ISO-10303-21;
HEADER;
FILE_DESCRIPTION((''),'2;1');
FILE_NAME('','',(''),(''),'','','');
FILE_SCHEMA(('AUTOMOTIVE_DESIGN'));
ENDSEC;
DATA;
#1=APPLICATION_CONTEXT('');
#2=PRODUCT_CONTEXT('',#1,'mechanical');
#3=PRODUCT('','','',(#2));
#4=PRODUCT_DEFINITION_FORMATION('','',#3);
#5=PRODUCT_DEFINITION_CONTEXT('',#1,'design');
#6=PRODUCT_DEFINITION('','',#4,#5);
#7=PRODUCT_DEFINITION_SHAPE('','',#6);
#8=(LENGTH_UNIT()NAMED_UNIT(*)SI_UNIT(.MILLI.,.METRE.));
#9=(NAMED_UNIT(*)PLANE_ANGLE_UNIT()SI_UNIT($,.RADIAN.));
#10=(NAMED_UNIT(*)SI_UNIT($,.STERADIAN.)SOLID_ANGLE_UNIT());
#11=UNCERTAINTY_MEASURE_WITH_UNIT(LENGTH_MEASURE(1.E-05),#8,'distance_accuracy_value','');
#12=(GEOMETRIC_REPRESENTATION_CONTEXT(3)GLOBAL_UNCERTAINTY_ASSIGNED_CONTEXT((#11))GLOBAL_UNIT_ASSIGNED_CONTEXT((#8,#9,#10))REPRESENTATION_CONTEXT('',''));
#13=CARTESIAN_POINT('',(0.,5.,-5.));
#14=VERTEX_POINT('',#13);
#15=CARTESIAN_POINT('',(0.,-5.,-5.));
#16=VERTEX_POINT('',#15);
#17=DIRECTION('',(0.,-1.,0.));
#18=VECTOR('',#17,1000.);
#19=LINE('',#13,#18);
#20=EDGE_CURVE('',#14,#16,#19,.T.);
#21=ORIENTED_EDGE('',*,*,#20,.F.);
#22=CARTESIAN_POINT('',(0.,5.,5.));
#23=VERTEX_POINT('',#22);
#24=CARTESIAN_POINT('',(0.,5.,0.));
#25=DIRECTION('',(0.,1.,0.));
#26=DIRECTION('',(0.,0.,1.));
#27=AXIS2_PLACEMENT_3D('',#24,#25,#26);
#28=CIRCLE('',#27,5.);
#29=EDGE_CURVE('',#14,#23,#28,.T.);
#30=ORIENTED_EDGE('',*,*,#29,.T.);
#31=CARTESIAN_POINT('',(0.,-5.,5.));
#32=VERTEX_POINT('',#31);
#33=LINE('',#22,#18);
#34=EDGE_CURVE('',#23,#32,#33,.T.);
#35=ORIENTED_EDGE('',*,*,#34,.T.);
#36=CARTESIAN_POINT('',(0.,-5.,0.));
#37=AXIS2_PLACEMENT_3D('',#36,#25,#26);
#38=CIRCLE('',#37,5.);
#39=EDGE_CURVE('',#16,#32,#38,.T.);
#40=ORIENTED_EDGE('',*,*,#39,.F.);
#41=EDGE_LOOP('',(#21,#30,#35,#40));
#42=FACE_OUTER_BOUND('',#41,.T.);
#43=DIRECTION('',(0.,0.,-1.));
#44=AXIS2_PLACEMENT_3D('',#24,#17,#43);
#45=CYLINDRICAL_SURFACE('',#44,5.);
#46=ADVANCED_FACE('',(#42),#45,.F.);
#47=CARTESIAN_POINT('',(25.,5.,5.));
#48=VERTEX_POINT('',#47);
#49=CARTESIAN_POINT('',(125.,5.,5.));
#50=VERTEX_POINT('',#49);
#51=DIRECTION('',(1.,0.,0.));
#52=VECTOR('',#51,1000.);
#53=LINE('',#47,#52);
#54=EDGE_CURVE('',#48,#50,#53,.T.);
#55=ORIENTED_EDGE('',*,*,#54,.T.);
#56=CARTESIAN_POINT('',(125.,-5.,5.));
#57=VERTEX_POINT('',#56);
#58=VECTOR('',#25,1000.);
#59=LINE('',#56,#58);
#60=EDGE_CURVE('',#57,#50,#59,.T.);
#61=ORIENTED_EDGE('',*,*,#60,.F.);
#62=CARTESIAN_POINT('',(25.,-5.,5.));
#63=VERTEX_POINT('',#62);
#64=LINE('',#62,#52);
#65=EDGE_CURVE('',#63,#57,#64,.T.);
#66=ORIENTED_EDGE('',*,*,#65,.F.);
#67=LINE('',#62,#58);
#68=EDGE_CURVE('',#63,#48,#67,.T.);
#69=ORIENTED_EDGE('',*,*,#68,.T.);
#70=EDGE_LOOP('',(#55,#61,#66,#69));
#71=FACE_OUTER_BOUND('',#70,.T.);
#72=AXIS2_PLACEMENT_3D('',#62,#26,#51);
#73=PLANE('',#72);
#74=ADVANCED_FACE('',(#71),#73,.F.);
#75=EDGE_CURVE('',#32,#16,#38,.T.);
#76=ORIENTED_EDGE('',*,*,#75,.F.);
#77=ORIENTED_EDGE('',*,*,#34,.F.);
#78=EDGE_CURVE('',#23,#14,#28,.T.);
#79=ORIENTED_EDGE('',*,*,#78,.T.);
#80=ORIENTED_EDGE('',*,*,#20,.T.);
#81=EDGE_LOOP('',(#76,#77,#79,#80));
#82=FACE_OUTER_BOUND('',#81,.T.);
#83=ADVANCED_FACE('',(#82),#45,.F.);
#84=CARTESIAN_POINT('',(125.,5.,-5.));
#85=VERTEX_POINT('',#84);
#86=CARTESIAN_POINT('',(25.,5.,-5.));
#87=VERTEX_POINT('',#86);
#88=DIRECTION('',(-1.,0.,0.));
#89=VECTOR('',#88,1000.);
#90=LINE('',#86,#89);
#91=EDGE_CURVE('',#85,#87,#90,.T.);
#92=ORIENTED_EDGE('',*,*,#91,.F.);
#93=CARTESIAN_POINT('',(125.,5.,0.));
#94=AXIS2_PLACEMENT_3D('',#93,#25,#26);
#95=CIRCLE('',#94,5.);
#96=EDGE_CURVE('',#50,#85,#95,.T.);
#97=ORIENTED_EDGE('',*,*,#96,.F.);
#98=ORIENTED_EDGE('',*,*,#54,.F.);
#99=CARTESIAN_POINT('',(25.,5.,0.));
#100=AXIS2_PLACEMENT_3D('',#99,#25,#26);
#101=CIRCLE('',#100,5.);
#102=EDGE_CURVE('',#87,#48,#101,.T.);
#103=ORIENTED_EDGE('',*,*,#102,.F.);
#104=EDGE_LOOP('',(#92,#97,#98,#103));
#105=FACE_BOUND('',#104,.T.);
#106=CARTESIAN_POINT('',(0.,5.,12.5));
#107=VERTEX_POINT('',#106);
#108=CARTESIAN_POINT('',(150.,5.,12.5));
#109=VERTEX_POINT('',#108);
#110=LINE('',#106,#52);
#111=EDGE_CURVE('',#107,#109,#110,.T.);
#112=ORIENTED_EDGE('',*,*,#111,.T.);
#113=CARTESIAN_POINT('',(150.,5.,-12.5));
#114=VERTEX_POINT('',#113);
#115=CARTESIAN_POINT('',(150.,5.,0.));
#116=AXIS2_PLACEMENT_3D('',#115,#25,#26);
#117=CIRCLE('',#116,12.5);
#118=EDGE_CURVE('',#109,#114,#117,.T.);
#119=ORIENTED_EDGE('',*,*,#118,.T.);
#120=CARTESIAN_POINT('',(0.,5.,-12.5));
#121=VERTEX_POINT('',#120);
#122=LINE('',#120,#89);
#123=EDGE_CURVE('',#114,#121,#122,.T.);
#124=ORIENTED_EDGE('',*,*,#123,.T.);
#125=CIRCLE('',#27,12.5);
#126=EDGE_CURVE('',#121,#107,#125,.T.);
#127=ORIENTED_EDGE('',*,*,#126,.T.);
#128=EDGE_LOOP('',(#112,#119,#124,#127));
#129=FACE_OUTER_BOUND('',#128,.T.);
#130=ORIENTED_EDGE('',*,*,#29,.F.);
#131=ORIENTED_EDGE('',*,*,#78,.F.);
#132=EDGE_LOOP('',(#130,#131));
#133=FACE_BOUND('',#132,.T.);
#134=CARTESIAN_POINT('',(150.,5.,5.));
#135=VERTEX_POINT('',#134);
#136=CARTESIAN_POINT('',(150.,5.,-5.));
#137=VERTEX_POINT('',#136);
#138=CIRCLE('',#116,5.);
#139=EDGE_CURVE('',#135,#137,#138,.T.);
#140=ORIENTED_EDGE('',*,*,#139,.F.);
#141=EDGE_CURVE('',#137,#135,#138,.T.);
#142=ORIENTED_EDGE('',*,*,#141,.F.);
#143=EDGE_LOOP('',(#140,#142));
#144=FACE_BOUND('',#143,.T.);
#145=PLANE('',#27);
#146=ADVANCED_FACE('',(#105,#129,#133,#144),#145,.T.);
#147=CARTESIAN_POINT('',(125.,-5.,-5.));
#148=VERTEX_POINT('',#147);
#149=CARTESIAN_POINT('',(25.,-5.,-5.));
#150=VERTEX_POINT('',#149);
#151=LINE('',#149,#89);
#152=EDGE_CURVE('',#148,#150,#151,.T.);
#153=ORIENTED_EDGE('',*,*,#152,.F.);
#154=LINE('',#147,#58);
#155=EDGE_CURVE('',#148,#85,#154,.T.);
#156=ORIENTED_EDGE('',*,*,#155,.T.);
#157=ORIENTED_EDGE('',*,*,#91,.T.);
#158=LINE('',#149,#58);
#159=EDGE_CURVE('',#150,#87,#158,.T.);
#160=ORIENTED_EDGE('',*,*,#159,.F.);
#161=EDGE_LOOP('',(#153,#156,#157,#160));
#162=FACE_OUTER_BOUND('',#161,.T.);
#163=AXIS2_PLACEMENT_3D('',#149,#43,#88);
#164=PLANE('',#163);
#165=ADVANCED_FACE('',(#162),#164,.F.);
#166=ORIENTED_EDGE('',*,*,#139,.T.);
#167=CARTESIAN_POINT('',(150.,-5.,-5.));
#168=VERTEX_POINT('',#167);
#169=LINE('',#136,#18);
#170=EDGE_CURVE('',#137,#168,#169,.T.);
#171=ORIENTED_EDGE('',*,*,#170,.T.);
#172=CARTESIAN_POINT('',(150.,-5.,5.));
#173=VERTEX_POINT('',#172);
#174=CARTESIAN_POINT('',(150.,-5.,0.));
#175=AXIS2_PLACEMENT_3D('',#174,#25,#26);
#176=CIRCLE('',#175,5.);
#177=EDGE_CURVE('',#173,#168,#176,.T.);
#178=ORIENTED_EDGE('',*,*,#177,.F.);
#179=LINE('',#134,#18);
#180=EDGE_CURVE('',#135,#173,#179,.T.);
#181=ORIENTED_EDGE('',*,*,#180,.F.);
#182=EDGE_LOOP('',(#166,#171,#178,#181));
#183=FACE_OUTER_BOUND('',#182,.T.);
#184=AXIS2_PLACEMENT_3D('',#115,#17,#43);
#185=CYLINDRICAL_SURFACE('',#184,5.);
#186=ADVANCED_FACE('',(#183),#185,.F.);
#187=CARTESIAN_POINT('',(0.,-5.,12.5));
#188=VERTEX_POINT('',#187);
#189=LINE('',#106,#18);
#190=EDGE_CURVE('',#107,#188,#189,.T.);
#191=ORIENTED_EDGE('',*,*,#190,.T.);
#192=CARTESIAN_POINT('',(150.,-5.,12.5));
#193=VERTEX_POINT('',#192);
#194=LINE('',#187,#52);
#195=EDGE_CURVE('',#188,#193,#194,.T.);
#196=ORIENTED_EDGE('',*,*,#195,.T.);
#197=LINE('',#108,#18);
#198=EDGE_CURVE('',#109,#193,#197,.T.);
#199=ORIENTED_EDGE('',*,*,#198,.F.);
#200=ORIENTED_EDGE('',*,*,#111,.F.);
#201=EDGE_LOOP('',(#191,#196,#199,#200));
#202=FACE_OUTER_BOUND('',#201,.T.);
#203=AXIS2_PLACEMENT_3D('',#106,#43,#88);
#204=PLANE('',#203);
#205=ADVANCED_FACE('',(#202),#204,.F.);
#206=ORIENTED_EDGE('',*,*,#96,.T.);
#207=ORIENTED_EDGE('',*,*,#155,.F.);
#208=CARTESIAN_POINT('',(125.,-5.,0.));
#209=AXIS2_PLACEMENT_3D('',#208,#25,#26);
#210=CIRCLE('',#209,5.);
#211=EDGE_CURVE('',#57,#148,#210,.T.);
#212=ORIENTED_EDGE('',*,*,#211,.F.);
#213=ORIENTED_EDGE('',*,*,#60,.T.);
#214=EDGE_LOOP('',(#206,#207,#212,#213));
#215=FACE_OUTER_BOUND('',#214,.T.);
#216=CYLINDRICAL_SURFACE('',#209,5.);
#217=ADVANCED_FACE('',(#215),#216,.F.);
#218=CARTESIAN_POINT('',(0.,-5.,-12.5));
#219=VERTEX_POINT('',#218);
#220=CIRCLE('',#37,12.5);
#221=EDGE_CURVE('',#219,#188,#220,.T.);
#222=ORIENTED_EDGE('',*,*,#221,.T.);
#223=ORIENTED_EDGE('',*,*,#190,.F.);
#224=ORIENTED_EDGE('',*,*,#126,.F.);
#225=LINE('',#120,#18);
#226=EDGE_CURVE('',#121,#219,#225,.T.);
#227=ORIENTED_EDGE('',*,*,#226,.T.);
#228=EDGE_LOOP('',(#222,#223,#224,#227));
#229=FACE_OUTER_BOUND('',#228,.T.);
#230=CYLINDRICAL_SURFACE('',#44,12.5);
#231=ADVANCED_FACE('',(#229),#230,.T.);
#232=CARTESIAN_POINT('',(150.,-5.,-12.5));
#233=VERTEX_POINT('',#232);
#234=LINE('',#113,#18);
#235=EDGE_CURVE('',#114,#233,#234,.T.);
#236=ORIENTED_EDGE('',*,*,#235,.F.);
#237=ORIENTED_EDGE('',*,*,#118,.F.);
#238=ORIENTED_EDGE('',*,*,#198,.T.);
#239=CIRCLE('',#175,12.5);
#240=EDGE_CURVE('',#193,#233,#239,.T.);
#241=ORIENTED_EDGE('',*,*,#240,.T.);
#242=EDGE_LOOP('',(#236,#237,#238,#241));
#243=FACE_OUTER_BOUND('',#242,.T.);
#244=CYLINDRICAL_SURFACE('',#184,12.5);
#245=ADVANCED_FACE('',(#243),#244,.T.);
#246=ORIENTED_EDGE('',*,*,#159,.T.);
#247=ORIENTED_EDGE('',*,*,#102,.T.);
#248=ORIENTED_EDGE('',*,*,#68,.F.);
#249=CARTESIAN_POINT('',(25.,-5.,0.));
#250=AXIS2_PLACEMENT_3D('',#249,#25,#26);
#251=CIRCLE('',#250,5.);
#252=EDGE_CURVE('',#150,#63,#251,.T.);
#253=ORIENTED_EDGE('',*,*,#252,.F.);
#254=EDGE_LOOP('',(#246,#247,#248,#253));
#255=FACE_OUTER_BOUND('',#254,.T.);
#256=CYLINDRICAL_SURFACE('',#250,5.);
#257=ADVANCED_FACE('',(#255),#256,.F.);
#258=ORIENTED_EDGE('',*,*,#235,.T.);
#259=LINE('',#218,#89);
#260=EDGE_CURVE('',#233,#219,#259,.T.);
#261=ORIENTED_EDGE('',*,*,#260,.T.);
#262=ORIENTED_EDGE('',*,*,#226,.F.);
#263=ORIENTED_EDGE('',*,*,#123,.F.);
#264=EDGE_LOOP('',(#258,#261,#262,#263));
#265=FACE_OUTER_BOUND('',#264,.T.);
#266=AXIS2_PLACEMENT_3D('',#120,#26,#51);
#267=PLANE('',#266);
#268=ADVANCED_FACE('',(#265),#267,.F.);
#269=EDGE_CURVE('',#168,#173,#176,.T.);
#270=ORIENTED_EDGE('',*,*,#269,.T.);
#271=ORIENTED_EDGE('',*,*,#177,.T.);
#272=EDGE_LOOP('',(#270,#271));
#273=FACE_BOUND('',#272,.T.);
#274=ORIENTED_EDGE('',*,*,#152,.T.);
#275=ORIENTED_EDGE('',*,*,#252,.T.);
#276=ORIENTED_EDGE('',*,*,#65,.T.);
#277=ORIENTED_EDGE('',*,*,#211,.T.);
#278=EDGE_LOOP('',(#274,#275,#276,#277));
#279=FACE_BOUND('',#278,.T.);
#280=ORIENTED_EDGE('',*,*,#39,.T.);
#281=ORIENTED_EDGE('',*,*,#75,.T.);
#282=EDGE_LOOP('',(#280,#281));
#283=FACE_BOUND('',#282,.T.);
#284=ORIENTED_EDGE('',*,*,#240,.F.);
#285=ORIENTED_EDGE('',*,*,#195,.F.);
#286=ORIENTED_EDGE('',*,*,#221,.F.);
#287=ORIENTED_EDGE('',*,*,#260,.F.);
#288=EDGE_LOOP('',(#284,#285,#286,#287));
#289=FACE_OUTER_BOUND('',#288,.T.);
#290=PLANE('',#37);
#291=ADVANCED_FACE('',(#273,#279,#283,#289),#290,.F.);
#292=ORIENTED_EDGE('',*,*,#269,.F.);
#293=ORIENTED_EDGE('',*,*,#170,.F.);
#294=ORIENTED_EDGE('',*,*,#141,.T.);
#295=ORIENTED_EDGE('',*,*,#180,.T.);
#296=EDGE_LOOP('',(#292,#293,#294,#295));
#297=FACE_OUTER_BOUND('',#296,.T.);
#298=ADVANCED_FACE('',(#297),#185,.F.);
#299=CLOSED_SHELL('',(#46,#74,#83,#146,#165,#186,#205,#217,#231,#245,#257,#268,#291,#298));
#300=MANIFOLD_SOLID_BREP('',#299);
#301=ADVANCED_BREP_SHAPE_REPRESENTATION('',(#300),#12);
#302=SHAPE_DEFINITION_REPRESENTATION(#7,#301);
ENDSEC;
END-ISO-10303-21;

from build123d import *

# Parameters (mm, degrees)
SKETCH1_R           = 5
BOSS_EXTRUDE1_DEPTH = 5
CUT_EXTRUDE1_DEPTH  = 10


with BuildPart() as part:
    # Sketch1 → Boss-Extrude1 (new, symmetric)
    with BuildSketch(Plane(origin=(0, 0, 0), x_dir=(1, 0, 0), z_dir=(0, 1, 0))):
        with BuildLine():
            Line((0, 12.5), (150, 12.5))
            ThreePointArc((150, 12.5), (162.5, 0), (150, -12.5))
            Line((150, -12.5), (0, -12.5))
            ThreePointArc((0, -12.5), (-12.5, 0), (0, 12.5))
        make_face()
        with Locations(Location((0, 0, 0), (0, 0, 270))):
            Circle(SKETCH1_R, mode=Mode.SUBTRACT)
        with Locations(Location((150, 0, 0), (0, 0, 270))):
            Circle(SKETCH1_R, mode=Mode.SUBTRACT)
    extrude(amount=BOSS_EXTRUDE1_DEPTH, both=True)

    # Sketch2 → Cut-Extrude1 (cut)
    with BuildSketch(Plane(origin=(0, 5, 0), x_dir=(1, 0, 0), z_dir=(0, 1, 0))):
        with BuildLine():
            Line((25, 5), (125, 5))
            ThreePointArc((125, 5), (130, 0), (125, -5))
            Line((125, -5), (25, -5))
            ThreePointArc((25, -5), (20, 0), (25, 5))
        make_face()
    extrude(amount=-CUT_EXTRUDE1_DEPTH, mode=Mode.SUBTRACT)


solid = part.part
